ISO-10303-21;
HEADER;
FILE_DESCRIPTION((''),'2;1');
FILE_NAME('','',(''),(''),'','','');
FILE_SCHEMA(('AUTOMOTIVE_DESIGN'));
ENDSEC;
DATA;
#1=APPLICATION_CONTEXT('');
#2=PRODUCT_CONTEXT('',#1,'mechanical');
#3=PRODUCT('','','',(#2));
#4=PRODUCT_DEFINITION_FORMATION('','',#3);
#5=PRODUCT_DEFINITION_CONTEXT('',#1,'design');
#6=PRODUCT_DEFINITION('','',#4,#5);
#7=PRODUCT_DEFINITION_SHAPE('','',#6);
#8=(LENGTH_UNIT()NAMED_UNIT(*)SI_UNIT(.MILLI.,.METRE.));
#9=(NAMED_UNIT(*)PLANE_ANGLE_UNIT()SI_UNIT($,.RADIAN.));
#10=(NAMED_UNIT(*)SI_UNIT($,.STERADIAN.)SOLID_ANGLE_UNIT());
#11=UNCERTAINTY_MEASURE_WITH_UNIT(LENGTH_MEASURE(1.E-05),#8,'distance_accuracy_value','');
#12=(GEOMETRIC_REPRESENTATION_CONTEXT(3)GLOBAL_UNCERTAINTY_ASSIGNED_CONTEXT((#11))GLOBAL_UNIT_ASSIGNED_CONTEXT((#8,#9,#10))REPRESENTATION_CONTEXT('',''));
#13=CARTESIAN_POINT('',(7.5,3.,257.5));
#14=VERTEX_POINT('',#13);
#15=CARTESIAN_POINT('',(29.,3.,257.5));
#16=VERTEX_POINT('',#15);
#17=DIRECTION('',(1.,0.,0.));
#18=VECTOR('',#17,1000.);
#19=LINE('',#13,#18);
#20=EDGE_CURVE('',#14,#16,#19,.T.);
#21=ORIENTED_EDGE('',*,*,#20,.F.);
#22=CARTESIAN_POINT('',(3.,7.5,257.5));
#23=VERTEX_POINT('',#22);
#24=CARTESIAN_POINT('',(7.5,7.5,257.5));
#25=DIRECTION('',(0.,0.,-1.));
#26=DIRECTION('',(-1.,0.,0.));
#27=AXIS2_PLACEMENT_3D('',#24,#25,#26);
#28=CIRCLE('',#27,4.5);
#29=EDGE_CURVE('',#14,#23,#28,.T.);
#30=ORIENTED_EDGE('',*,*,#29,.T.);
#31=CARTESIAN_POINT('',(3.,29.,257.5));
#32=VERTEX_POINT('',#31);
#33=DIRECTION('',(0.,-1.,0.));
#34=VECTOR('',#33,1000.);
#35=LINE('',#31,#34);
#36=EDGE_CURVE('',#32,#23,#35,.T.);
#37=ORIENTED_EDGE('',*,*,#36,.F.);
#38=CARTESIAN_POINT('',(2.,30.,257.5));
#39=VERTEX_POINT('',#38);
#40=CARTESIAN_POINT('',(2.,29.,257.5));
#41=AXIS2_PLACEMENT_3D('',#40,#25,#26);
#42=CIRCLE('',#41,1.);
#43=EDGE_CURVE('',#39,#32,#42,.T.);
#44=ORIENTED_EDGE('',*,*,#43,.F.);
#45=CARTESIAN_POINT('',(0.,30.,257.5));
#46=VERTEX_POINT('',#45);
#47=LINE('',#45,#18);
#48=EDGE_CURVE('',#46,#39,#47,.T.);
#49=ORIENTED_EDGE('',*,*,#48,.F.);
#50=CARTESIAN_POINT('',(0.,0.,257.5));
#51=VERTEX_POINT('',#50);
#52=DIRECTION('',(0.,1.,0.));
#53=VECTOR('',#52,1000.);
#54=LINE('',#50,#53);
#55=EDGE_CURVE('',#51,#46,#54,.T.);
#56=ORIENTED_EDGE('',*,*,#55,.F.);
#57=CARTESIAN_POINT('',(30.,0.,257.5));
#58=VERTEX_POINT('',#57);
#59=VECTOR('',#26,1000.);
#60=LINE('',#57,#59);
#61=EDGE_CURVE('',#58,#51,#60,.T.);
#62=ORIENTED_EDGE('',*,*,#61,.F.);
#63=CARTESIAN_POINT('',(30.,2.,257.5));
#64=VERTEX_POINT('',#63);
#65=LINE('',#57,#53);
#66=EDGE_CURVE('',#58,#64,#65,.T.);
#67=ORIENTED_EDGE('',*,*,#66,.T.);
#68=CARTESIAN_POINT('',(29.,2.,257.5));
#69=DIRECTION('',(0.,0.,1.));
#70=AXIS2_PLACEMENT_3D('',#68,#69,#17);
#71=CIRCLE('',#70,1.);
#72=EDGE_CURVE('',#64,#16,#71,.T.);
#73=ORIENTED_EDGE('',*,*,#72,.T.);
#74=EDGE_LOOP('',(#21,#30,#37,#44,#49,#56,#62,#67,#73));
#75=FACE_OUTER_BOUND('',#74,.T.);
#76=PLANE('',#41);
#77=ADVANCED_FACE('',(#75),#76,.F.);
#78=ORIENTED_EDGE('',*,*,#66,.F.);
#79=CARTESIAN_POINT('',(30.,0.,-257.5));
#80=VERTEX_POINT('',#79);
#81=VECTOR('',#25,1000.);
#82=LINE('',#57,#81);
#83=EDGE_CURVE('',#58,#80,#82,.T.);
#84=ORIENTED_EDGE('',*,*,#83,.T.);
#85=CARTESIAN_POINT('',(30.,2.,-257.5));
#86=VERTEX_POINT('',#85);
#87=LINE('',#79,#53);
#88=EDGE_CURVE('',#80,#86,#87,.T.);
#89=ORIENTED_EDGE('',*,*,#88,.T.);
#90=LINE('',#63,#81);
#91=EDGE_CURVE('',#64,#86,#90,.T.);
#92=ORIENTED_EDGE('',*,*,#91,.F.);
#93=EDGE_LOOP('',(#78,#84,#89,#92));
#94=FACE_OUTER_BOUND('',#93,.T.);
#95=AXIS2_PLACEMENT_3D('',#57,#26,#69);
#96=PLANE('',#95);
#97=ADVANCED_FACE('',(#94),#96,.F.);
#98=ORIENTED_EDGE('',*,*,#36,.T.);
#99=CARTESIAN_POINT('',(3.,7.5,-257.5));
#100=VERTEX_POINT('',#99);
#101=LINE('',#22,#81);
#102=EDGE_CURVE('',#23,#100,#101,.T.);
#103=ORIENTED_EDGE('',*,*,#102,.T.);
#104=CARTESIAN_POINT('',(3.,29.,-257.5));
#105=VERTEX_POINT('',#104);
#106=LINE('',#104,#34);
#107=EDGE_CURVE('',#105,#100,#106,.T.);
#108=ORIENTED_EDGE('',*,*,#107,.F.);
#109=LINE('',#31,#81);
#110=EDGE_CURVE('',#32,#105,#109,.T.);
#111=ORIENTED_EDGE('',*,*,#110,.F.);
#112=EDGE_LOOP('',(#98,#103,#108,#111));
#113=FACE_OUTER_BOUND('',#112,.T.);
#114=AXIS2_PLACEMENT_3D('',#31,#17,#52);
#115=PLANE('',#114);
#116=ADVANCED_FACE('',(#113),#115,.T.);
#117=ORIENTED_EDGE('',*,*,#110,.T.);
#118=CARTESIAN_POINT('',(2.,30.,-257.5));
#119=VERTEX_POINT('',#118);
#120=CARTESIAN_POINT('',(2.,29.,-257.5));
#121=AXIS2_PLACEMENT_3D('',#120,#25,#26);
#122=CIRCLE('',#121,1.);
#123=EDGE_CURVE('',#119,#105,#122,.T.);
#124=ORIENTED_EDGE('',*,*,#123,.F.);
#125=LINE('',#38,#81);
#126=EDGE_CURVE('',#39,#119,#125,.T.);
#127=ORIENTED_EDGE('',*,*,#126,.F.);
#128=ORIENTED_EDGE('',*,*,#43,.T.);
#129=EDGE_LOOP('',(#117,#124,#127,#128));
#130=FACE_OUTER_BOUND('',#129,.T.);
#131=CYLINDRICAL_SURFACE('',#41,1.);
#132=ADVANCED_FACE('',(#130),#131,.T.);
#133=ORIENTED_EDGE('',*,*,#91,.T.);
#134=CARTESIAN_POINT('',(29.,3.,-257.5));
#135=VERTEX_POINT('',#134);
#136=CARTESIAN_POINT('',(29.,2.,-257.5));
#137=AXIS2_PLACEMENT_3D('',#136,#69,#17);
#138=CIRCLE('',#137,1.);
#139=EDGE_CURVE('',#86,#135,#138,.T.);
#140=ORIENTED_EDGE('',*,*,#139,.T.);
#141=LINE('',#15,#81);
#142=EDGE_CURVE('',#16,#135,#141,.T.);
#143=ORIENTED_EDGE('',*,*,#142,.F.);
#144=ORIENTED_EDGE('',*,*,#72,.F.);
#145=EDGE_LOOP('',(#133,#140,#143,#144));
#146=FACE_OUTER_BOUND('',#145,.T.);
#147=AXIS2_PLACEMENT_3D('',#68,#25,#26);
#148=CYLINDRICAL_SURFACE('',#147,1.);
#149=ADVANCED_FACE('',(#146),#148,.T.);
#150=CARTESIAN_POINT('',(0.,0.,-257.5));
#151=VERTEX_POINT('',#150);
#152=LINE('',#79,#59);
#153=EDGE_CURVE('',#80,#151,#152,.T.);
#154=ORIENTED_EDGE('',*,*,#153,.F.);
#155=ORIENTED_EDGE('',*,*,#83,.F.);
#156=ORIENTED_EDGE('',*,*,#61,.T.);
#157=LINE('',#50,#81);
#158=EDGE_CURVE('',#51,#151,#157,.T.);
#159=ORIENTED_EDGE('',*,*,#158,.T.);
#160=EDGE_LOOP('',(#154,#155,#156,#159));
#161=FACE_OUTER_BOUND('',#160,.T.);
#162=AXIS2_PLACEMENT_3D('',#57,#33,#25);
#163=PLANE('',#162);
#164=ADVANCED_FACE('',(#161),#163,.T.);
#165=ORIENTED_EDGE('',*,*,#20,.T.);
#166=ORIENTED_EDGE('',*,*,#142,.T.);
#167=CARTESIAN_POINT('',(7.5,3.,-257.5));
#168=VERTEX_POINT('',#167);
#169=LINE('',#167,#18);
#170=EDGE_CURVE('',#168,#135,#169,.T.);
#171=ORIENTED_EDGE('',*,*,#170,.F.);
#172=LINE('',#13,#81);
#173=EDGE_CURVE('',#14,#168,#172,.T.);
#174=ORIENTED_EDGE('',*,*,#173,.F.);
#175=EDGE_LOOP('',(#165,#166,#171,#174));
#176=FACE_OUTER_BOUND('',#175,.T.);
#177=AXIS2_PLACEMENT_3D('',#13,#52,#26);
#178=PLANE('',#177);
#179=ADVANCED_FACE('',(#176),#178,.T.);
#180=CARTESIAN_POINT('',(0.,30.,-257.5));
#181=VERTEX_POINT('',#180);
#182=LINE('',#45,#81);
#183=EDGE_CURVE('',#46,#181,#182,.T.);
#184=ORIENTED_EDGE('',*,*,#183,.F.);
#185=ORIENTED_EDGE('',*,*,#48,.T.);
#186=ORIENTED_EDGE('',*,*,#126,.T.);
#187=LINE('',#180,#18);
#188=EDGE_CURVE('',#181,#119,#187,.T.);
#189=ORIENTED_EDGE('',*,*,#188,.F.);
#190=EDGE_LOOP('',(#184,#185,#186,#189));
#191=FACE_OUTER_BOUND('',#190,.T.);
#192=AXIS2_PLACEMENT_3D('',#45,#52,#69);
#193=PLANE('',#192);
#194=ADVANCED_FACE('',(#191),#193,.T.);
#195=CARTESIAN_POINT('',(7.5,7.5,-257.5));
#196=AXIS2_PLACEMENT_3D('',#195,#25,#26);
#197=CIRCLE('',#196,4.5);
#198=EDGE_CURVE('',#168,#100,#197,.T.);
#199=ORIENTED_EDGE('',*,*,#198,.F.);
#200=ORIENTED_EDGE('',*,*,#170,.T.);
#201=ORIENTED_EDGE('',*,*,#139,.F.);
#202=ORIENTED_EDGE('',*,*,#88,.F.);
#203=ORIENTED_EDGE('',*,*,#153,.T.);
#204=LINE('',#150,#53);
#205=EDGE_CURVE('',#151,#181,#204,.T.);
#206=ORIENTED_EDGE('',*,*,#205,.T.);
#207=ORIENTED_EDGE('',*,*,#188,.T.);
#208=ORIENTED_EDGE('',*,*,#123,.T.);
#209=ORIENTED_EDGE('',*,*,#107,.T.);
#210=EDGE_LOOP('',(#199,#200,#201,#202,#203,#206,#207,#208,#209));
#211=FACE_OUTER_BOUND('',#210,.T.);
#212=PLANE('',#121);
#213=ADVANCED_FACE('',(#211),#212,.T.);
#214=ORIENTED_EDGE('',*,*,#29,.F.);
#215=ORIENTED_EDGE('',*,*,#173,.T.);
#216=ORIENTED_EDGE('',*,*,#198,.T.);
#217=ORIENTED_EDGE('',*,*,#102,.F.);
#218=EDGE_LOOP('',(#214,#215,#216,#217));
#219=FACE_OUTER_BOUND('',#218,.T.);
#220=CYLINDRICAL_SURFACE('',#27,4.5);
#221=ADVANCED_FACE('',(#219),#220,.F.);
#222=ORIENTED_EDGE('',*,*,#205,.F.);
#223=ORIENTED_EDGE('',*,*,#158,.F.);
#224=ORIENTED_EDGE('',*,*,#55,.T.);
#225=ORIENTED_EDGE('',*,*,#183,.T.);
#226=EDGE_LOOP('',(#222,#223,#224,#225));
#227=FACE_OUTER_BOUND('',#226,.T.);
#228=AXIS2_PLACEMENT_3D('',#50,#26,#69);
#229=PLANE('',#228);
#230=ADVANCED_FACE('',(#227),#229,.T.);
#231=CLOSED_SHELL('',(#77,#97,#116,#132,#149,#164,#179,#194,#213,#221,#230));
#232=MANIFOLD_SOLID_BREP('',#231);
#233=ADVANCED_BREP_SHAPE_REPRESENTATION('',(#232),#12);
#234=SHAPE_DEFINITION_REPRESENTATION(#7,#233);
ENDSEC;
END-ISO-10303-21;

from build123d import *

# Parameters (mm, degrees)
BOSS_EXTRUDE1_DEPTH = 257.5


with BuildPart() as part:
    # Sketch1 → Boss-Extrude1 (new, symmetric)
    with BuildSketch(Plane.XY):
        with BuildLine():
            Line((0, 0), (0, 30))
            Line((0, 30), (2, 30))
            ThreePointArc((2, 30), (2.707106781, 29.707106781), (3, 29))
            Line((3, 29), (3, 7.5))
            ThreePointArc((3, 7.5), (4.318019485, 4.318019485), (7.5, 3))
            Line((7.5, 3), (29, 3))
            ThreePointArc((29, 3), (29.707106781, 2.707106781), (30, 2))
            Line((30, 2), (30, 0))
            Line((30, 0), (0, 0))
        make_face()
    extrude(amount=BOSS_EXTRUDE1_DEPTH, both=True)


solid = part.part
